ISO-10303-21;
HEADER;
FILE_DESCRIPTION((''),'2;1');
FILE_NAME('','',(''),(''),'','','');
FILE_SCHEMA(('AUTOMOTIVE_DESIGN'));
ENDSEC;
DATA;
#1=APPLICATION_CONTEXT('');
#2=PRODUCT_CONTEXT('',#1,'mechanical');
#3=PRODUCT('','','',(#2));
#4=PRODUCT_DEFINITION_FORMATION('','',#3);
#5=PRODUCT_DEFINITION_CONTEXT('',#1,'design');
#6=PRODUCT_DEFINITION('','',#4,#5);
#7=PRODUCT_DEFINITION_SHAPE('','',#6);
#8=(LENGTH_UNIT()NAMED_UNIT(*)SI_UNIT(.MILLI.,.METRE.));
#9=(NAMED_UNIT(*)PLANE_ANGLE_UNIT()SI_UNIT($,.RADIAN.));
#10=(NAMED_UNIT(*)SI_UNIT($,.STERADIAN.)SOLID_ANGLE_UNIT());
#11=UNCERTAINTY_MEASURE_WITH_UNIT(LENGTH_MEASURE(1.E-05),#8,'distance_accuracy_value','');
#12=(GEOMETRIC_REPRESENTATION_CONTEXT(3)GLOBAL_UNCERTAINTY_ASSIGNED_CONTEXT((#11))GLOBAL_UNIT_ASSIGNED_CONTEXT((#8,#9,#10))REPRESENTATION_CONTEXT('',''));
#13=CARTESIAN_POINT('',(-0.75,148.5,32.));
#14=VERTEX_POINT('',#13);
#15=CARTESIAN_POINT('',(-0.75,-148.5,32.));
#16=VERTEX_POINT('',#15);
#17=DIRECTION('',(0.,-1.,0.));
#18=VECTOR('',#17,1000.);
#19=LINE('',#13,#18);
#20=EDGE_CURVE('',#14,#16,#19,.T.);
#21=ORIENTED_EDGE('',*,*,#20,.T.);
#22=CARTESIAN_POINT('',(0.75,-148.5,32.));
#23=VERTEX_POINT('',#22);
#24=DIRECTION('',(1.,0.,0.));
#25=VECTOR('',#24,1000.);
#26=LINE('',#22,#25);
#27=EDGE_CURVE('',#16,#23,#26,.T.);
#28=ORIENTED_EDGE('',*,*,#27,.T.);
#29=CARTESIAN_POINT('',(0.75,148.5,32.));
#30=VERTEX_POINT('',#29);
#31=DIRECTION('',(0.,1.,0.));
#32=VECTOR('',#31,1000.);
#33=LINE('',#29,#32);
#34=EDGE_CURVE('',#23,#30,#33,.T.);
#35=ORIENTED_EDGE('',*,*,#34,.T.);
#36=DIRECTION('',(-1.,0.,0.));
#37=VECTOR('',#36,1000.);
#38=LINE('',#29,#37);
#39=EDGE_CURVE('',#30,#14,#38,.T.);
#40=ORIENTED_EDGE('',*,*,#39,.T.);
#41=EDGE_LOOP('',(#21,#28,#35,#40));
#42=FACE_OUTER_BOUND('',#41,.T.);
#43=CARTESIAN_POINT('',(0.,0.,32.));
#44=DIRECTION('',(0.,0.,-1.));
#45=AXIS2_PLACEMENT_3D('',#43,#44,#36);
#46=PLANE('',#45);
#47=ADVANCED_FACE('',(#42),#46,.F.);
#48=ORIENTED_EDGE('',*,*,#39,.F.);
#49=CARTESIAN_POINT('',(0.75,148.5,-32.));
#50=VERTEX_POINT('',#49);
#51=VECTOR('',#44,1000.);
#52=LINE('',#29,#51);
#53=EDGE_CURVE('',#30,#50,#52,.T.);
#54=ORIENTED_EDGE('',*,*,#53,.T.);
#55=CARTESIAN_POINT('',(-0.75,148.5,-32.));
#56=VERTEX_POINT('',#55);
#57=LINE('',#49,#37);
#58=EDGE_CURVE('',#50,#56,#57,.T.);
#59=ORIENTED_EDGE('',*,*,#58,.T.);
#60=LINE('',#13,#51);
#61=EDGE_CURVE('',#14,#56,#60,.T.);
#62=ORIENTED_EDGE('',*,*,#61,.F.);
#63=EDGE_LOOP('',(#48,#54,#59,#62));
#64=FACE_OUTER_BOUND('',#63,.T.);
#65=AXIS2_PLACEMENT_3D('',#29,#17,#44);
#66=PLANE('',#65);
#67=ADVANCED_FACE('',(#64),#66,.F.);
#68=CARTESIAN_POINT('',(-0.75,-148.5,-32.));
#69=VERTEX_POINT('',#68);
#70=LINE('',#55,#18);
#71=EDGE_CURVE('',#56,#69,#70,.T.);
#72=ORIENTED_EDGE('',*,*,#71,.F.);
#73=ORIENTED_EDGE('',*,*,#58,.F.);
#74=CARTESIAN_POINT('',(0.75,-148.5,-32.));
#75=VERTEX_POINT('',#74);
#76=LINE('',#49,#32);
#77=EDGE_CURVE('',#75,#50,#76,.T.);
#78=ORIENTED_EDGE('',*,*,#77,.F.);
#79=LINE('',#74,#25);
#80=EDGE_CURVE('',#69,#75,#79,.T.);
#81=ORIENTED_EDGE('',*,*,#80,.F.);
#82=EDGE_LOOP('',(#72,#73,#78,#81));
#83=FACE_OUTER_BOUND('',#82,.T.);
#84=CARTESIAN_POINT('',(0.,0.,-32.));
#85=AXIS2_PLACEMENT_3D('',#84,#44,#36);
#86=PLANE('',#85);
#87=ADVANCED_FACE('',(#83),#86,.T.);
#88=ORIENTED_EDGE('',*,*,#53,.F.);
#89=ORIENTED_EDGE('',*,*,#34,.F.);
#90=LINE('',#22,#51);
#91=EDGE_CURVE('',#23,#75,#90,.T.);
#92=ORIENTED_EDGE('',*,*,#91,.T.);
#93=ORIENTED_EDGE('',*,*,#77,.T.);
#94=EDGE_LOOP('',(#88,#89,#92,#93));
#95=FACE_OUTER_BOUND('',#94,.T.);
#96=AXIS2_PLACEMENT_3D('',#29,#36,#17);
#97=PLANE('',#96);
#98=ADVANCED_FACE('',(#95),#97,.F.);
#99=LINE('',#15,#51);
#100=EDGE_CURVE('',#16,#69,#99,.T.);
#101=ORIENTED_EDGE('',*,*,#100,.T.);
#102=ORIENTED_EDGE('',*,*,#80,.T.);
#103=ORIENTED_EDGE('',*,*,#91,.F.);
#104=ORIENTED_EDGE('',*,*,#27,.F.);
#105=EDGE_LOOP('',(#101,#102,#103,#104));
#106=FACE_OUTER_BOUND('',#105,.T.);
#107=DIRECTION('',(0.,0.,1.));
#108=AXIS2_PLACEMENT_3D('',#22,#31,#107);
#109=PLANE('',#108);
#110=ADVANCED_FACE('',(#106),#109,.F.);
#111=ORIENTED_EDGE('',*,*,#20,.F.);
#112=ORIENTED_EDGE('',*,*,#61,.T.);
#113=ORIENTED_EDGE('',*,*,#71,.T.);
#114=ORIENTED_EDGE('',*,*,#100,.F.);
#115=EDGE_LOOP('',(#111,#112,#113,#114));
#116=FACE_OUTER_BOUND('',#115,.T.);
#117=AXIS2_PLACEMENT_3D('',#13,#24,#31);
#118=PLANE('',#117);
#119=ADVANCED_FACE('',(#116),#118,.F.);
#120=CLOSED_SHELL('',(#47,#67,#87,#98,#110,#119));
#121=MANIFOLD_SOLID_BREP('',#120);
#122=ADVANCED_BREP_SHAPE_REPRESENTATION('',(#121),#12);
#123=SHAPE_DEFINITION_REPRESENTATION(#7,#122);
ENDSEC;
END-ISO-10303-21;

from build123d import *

# Parameters (mm, degrees)
SKETCH1_W           = 1.5
SKETCH1_H           = 297
BOSS_EXTRUDE1_DEPTH = 32


with BuildPart() as part:
    # Sketch1 → Boss-Extrude1 (new, symmetric)
    with BuildSketch(Plane.XY):
        Rectangle(SKETCH1_W, SKETCH1_H)
    extrude(amount=BOSS_EXTRUDE1_DEPTH, both=True)


solid = part.part
